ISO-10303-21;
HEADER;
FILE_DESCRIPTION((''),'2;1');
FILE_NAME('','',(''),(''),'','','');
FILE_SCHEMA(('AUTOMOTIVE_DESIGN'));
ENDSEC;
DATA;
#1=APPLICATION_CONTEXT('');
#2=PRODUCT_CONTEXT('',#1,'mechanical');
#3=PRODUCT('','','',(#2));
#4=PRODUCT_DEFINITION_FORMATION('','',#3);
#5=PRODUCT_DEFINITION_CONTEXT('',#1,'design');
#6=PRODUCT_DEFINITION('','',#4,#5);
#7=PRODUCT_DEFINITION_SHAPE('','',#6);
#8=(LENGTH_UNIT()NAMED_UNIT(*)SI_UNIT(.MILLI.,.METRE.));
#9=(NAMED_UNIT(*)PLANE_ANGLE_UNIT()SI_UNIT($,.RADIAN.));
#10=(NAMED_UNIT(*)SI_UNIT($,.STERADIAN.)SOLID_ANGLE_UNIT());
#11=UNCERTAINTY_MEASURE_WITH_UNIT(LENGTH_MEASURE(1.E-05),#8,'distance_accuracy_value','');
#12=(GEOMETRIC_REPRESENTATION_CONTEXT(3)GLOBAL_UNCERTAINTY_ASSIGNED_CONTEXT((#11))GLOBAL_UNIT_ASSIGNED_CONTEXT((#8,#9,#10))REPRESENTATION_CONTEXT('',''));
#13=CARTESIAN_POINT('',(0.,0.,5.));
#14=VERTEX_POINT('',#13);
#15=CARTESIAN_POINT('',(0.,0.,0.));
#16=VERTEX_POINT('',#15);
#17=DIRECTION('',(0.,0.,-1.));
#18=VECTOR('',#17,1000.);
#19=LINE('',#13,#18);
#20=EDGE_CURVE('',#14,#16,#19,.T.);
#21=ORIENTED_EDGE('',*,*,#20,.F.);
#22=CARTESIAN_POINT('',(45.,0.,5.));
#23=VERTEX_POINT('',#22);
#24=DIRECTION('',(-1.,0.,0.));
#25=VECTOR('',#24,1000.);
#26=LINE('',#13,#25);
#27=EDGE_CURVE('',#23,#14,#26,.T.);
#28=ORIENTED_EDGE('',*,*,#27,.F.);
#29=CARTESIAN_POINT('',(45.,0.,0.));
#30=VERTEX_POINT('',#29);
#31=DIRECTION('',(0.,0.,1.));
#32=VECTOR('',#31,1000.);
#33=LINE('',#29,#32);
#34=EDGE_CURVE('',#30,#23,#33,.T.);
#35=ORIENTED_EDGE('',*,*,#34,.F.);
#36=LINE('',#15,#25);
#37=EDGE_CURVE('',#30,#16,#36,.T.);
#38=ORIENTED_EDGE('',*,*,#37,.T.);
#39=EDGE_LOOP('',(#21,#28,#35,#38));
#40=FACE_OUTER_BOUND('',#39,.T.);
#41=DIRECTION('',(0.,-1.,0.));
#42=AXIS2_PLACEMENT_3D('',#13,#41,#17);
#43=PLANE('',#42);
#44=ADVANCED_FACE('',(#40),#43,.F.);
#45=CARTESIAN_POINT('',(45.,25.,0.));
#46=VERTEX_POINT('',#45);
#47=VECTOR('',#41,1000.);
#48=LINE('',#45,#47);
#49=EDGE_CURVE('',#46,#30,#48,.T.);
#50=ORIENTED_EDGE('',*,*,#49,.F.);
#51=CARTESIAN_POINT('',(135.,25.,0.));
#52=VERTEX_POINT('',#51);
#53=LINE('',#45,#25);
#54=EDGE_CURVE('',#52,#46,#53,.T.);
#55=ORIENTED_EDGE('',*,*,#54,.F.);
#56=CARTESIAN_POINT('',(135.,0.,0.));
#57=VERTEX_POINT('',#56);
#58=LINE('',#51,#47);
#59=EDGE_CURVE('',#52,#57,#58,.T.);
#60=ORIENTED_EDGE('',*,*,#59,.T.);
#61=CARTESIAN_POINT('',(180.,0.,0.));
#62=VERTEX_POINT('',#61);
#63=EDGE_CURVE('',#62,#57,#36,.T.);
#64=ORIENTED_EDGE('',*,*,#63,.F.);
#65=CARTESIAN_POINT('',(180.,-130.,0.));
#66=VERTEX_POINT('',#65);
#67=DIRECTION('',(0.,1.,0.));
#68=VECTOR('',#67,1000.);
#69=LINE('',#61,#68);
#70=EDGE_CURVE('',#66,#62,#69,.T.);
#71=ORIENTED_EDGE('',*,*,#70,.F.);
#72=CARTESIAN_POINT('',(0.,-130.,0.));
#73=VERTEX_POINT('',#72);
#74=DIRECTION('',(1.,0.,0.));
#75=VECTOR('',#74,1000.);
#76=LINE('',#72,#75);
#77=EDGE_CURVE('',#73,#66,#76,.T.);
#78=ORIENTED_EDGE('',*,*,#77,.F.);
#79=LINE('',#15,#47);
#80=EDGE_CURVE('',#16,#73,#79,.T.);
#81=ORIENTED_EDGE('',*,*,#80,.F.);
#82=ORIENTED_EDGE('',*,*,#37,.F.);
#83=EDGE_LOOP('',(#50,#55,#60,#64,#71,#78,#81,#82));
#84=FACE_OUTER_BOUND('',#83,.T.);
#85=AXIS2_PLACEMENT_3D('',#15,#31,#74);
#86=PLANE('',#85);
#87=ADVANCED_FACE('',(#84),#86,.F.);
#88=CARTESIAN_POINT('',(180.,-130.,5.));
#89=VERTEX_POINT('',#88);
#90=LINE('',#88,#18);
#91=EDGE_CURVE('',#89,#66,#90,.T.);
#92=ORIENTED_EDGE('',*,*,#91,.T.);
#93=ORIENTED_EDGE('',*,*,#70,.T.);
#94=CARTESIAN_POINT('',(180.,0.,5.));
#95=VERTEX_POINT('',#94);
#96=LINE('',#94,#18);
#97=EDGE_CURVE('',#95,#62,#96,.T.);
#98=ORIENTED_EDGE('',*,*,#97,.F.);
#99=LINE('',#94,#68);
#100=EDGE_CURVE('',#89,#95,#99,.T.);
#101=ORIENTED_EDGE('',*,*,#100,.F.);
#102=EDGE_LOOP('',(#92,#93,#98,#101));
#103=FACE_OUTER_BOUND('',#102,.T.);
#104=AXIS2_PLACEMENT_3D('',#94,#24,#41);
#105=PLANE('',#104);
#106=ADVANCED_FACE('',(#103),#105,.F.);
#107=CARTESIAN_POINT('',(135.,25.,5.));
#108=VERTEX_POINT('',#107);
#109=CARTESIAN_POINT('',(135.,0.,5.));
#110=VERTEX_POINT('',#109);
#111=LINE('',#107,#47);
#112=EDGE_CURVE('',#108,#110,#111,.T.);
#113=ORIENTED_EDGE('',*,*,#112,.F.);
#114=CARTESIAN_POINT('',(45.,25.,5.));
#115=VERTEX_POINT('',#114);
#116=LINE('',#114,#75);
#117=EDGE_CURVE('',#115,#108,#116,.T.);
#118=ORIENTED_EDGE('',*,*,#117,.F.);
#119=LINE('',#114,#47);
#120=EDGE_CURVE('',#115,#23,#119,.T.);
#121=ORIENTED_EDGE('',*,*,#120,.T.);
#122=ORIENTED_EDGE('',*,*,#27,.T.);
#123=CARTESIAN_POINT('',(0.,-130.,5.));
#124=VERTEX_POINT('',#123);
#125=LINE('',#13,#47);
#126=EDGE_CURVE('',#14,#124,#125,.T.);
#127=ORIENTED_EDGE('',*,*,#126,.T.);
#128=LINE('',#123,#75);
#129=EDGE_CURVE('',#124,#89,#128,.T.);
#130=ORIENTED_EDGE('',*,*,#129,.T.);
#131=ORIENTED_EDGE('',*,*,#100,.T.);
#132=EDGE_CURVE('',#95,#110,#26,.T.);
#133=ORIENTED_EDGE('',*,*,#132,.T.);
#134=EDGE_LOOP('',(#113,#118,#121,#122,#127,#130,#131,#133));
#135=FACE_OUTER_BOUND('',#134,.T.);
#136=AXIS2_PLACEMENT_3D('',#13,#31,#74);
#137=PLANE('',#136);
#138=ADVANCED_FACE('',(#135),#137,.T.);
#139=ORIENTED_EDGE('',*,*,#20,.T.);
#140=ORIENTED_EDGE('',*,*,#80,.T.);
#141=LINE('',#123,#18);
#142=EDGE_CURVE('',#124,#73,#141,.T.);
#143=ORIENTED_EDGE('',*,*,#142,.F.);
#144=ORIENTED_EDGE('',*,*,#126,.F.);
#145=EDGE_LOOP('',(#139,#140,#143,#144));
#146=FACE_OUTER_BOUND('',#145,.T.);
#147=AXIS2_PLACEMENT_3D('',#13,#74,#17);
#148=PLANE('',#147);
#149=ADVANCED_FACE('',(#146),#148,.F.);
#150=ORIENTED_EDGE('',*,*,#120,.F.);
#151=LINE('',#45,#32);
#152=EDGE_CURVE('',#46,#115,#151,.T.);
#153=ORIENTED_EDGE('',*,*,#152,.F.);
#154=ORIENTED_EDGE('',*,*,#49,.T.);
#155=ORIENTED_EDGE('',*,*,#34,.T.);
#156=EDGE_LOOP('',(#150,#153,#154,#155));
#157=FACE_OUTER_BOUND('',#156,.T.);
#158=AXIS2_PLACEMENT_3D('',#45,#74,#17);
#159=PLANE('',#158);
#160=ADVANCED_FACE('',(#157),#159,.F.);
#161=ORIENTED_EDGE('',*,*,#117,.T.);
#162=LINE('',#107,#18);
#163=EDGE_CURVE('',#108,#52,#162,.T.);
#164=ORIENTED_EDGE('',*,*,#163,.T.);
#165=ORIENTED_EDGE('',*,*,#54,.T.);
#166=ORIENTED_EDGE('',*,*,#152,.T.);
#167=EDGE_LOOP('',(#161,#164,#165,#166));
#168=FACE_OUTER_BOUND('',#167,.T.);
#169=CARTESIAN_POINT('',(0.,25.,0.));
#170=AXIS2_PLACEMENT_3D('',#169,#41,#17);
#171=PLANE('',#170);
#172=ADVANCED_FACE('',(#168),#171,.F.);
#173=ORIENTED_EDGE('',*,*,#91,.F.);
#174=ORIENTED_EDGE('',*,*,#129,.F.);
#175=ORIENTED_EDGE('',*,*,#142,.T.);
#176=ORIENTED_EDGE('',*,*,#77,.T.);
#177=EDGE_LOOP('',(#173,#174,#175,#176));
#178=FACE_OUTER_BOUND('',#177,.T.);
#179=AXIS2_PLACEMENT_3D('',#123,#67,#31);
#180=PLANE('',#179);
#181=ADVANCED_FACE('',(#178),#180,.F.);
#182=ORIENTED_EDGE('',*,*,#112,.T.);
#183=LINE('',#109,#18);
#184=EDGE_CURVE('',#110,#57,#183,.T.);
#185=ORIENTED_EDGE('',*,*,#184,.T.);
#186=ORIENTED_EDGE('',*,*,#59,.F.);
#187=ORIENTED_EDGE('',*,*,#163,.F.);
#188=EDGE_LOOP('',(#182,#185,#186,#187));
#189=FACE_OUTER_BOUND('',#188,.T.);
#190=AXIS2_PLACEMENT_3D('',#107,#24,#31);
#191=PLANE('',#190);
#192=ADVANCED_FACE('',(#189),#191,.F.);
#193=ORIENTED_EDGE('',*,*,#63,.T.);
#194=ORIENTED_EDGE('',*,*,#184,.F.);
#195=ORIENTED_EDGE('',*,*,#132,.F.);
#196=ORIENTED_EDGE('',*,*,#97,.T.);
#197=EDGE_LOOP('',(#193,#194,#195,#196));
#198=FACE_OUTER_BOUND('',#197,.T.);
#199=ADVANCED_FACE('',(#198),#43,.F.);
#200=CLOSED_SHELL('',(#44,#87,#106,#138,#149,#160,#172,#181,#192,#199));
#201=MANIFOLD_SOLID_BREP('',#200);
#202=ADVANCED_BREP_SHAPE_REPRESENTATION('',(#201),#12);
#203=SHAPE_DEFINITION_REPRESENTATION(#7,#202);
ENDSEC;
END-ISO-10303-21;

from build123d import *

# Parameters (mm, degrees)
SKETCH_1_W      = 180
SKETCH_1_H      = 130
EXTRUDE_1_DEPTH = 5
SKETCH_2_W      = 90
SKETCH_2_H      = 5
EXTRUDE_2_DEPTH = 25


with BuildPart() as part:
    # 草图1 → 凸台-拉伸1 (new body)
    with BuildSketch(Plane.XY):
        with Locations((90, -65)):
            Rectangle(SKETCH_1_W, SKETCH_1_H)
    extrude(amount=EXTRUDE_1_DEPTH)

    # 草图2 → 凸台-拉伸2 (add)
    with BuildSketch(Plane(origin=(0, 0, 0), x_dir=(1, 0, 0), z_dir=(0, 1, 0))):
        with Locations((90, -2.5)):
            Rectangle(SKETCH_2_W, SKETCH_2_H)
    extrude(amount=EXTRUDE_2_DEPTH)


solid = part.part
